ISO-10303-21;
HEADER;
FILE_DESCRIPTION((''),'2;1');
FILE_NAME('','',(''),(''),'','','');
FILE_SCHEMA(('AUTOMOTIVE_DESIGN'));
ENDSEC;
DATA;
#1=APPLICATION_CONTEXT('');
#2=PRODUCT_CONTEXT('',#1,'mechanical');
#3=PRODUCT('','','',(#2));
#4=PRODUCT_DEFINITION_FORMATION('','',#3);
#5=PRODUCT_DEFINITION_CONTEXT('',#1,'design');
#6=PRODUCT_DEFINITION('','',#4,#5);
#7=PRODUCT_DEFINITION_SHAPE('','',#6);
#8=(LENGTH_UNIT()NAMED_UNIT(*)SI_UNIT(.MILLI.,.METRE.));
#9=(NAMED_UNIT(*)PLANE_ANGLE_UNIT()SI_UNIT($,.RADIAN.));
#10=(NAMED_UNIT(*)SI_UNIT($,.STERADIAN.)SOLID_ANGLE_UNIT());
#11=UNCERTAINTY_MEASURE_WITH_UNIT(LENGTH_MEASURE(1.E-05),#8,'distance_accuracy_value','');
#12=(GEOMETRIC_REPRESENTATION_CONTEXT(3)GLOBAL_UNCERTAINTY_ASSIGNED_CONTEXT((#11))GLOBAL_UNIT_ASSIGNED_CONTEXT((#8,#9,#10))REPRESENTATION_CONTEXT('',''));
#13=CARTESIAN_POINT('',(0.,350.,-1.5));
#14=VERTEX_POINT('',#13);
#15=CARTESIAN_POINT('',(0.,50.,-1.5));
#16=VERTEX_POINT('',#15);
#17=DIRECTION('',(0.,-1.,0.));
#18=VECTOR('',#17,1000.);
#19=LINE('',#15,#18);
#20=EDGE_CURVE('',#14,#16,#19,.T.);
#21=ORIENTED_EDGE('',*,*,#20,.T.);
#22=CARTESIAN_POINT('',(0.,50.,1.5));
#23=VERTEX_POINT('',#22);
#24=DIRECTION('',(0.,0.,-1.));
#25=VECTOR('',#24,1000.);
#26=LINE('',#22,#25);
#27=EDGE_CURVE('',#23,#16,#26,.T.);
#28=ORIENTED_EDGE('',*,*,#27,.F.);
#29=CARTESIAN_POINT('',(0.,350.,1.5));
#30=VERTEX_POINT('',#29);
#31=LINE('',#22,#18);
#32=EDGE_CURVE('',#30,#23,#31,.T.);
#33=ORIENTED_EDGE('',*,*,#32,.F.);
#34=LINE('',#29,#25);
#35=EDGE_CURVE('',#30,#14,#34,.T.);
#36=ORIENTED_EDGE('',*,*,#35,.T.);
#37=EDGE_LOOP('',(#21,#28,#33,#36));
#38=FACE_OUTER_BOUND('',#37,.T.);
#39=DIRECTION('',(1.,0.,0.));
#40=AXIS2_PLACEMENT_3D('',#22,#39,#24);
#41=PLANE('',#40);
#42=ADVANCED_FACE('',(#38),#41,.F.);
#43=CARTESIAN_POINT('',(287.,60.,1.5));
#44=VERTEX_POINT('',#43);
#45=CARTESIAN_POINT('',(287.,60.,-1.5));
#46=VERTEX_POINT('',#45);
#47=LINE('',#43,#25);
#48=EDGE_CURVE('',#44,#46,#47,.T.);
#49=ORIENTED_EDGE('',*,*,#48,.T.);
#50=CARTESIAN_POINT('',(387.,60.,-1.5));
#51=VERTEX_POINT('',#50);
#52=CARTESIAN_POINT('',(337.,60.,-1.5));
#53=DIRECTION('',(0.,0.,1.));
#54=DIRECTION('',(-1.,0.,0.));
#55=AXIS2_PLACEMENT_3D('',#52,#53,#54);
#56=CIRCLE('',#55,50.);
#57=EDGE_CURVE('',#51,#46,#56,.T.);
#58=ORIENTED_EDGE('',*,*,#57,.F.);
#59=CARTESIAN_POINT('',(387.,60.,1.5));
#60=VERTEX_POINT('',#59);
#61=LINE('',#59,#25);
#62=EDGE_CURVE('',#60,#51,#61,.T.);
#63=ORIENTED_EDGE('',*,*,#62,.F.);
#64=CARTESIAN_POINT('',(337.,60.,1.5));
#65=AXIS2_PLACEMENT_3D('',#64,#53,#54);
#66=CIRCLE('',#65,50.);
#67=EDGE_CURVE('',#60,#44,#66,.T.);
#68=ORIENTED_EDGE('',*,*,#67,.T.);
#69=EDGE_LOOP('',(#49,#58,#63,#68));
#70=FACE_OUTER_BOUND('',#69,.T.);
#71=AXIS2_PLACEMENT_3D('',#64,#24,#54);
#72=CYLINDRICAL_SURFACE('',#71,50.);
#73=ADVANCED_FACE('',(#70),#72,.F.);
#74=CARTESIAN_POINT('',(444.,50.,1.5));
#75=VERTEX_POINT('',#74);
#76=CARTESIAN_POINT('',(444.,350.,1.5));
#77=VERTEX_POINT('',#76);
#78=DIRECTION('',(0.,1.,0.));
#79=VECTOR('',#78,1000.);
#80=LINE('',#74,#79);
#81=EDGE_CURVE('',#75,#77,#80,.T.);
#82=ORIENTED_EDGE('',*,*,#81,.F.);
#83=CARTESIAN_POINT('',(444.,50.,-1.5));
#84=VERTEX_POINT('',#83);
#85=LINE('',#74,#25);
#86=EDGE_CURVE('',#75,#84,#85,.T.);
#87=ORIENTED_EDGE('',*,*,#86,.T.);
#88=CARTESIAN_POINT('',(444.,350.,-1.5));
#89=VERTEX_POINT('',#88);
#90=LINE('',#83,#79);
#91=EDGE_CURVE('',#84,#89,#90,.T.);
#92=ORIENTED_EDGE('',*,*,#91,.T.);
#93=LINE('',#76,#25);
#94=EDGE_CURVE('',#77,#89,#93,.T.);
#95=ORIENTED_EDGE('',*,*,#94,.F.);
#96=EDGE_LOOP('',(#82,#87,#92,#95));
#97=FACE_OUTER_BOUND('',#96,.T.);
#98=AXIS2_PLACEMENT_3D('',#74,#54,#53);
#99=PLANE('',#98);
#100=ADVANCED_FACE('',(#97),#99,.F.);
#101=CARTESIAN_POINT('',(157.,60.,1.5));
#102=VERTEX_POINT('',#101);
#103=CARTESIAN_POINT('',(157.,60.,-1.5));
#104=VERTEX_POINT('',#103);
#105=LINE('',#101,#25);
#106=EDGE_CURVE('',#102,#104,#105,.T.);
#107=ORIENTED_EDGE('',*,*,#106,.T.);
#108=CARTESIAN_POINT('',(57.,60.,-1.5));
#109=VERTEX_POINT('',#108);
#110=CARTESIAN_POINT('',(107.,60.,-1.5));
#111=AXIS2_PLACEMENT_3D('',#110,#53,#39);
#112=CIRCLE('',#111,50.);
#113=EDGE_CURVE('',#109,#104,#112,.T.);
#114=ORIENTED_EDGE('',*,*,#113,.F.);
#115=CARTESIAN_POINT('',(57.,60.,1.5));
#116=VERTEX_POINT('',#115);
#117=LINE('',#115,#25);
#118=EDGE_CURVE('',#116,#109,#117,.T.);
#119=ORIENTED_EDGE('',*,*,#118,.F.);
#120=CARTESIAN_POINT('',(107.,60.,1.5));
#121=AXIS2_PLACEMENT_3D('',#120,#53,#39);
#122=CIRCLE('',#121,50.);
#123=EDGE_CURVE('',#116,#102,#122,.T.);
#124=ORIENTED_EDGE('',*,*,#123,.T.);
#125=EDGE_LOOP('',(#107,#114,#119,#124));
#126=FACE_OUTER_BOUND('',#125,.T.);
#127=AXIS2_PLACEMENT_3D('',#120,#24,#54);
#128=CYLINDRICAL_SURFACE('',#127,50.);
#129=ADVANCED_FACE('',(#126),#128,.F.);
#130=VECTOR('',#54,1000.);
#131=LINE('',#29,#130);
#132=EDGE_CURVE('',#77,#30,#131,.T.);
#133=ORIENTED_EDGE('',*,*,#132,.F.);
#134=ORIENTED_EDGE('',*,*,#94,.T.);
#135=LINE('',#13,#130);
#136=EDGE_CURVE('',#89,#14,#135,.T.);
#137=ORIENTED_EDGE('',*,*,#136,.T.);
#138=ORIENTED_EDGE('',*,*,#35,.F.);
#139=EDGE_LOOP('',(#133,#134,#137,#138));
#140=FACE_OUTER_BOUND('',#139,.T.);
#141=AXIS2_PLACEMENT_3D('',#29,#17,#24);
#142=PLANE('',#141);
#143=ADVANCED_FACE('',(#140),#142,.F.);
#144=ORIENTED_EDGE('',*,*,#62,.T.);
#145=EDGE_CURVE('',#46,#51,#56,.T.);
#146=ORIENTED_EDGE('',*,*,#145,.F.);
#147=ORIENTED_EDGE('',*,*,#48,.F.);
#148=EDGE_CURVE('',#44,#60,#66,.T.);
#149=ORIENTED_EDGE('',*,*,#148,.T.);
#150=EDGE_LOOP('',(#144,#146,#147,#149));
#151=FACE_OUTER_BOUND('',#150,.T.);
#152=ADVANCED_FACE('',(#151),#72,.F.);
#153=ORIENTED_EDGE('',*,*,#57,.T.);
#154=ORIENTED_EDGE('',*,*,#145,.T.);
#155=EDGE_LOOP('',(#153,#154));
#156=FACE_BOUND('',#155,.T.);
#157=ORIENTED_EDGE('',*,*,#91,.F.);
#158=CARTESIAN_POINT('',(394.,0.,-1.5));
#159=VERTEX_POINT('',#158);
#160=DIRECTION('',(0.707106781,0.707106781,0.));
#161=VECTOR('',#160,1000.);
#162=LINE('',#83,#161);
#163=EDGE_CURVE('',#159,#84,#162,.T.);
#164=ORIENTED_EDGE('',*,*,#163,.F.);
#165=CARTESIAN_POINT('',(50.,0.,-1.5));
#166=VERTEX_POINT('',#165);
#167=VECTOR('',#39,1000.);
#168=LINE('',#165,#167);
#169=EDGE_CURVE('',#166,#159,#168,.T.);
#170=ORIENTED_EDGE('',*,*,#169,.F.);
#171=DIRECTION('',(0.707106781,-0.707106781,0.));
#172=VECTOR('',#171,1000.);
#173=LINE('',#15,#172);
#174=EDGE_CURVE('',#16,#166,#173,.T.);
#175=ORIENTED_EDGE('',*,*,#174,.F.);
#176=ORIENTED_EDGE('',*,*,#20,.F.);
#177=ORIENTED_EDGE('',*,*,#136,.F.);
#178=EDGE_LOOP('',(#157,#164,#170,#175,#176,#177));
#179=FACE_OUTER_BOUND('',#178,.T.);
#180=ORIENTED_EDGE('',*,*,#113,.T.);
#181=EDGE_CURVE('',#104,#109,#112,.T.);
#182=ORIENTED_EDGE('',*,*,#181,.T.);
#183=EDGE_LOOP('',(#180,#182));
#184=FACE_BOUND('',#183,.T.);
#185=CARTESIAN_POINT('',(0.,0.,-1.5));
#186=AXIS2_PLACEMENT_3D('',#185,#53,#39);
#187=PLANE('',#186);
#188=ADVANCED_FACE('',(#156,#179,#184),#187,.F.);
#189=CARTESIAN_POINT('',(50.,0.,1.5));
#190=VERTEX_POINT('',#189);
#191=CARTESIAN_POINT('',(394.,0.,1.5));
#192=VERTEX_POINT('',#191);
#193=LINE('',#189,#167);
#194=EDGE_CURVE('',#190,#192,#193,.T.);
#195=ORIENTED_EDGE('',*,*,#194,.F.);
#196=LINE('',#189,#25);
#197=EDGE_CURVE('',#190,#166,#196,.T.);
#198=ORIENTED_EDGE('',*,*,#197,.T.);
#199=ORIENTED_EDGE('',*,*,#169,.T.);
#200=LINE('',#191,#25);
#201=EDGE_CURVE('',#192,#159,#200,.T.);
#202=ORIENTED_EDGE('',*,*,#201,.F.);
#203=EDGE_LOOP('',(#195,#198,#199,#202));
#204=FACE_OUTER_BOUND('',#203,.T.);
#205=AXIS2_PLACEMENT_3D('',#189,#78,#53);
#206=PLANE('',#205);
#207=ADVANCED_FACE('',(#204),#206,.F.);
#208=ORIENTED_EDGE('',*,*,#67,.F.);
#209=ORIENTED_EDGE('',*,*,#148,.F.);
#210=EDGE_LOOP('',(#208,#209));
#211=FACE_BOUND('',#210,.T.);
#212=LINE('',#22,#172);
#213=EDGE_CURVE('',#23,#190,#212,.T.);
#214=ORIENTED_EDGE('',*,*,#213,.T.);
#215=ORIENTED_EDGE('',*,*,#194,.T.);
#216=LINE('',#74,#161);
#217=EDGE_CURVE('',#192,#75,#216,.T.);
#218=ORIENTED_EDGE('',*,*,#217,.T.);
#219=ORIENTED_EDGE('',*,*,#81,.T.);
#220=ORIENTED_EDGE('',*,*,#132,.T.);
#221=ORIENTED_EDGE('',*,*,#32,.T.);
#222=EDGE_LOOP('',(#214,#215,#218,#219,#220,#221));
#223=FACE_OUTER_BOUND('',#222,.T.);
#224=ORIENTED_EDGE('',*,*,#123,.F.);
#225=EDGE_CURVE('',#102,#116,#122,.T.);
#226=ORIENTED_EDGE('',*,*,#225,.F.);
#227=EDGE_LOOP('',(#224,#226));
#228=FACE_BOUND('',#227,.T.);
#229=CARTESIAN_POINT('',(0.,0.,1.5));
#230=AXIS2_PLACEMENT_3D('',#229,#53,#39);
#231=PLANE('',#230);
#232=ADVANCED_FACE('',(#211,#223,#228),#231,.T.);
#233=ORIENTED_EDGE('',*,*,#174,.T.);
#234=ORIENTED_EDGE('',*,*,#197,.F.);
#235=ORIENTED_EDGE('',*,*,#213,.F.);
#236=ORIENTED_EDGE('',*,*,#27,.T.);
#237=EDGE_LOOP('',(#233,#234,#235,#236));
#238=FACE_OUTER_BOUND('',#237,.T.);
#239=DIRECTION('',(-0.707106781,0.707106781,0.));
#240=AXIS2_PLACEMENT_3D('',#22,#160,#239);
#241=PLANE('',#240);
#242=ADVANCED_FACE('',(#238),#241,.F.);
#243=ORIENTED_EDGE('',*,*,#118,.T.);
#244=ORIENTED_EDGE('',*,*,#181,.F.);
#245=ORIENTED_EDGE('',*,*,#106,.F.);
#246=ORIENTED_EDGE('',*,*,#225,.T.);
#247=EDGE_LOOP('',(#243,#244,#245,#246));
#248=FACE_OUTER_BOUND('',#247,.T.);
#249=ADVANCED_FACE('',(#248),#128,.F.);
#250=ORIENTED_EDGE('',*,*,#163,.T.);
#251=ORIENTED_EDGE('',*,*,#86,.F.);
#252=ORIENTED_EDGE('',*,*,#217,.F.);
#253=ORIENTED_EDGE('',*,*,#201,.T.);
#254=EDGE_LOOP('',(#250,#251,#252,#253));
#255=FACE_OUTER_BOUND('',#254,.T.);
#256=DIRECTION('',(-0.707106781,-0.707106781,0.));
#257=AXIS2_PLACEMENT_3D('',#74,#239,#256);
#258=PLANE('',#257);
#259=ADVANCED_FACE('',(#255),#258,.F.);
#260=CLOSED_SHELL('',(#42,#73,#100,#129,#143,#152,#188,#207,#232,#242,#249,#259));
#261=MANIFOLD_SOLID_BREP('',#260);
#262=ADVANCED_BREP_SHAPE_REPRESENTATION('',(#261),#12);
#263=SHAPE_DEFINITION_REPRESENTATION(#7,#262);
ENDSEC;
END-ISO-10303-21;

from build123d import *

# Parameters (mm, degrees)
SKETCH1_R           = 50
BOSS_EXTRUDE1_DEPTH = 1.5


with BuildPart() as part:
    # Sketch1 → Boss-Extrude1 (new, symmetric)
    with BuildSketch(Plane.XY):
        Polygon((50, 0), (394, 0), (444, 50), (444, 350), (0, 350), (0, 50), align=None)
        with Locations((107, 60)):
            Circle(SKETCH1_R, mode=Mode.SUBTRACT)
        with Locations(Location((337, 60, 0), (0, 0, 180))):
            Circle(SKETCH1_R, mode=Mode.SUBTRACT)
    extrude(amount=BOSS_EXTRUDE1_DEPTH, both=True)


solid = part.part
